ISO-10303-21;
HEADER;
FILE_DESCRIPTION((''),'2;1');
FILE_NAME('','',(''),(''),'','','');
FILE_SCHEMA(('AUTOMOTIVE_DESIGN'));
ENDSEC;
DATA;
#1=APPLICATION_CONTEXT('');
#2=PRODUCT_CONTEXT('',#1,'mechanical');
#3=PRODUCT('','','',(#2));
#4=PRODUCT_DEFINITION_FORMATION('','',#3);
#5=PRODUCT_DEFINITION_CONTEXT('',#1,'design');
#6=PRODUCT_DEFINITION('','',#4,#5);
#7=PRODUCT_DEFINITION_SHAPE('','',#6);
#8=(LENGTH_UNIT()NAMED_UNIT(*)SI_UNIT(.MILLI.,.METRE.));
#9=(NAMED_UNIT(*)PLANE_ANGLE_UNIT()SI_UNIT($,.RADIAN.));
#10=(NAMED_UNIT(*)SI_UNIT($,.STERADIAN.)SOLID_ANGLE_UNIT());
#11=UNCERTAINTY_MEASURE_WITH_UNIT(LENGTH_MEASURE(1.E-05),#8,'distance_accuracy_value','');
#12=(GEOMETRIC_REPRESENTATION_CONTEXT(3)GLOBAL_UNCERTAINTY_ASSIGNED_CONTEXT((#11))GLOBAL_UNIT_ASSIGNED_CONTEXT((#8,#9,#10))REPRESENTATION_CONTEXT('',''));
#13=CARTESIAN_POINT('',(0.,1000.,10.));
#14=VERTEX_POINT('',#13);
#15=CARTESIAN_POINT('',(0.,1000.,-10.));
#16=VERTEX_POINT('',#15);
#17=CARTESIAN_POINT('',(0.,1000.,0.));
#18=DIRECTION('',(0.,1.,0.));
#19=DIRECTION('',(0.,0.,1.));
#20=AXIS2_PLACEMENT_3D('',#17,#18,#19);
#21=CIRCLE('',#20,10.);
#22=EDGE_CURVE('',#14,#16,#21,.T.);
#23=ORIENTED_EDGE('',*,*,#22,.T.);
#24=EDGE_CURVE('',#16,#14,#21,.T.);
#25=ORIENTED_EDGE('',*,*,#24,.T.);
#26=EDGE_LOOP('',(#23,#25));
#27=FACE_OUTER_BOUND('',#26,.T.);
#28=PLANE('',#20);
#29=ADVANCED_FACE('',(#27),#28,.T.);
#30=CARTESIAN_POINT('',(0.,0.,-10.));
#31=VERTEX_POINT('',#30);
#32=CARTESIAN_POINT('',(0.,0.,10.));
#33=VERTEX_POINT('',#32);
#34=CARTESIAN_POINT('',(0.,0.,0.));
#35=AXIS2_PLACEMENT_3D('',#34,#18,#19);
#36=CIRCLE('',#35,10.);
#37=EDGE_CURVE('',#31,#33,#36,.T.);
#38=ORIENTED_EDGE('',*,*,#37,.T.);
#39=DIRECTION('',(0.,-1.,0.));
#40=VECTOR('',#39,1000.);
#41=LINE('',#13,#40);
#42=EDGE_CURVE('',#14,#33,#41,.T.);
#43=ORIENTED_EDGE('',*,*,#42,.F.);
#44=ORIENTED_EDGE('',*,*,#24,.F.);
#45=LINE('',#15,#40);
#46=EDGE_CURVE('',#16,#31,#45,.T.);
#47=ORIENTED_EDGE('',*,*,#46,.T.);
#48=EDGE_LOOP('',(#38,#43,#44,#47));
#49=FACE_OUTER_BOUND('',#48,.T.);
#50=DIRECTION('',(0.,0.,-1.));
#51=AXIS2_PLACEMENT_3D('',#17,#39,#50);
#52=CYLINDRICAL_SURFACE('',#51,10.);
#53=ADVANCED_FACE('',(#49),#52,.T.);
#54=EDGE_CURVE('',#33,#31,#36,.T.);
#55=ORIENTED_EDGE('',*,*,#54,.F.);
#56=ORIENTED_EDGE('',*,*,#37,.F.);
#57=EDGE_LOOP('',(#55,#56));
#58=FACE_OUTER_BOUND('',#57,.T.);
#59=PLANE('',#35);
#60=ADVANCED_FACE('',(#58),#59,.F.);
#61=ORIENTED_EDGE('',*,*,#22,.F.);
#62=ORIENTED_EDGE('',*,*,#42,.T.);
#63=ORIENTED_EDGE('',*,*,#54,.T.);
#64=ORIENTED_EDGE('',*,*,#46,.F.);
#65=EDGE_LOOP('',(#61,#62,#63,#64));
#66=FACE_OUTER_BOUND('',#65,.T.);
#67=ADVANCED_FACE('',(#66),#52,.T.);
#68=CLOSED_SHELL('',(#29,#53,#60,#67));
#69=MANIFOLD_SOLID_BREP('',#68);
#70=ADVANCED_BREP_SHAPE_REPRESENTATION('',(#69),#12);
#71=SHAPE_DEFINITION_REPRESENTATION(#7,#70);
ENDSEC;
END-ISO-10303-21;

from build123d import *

# Parameters (mm, degrees)
SKETCH1_R           = 10
BOSS_EXTRUDE1_DEPTH = 1000


with BuildPart() as part:
    # Sketch1 → Boss-Extrude1 (new body)
    with BuildSketch(Plane(origin=(0, 0, 0), x_dir=(1, 0, 0), z_dir=(0, 1, 0))):
        with Locations(Location((0, 0, 0), (0, 0, 270))):
            Circle(SKETCH1_R)
    extrude(amount=BOSS_EXTRUDE1_DEPTH)


solid = part.part
